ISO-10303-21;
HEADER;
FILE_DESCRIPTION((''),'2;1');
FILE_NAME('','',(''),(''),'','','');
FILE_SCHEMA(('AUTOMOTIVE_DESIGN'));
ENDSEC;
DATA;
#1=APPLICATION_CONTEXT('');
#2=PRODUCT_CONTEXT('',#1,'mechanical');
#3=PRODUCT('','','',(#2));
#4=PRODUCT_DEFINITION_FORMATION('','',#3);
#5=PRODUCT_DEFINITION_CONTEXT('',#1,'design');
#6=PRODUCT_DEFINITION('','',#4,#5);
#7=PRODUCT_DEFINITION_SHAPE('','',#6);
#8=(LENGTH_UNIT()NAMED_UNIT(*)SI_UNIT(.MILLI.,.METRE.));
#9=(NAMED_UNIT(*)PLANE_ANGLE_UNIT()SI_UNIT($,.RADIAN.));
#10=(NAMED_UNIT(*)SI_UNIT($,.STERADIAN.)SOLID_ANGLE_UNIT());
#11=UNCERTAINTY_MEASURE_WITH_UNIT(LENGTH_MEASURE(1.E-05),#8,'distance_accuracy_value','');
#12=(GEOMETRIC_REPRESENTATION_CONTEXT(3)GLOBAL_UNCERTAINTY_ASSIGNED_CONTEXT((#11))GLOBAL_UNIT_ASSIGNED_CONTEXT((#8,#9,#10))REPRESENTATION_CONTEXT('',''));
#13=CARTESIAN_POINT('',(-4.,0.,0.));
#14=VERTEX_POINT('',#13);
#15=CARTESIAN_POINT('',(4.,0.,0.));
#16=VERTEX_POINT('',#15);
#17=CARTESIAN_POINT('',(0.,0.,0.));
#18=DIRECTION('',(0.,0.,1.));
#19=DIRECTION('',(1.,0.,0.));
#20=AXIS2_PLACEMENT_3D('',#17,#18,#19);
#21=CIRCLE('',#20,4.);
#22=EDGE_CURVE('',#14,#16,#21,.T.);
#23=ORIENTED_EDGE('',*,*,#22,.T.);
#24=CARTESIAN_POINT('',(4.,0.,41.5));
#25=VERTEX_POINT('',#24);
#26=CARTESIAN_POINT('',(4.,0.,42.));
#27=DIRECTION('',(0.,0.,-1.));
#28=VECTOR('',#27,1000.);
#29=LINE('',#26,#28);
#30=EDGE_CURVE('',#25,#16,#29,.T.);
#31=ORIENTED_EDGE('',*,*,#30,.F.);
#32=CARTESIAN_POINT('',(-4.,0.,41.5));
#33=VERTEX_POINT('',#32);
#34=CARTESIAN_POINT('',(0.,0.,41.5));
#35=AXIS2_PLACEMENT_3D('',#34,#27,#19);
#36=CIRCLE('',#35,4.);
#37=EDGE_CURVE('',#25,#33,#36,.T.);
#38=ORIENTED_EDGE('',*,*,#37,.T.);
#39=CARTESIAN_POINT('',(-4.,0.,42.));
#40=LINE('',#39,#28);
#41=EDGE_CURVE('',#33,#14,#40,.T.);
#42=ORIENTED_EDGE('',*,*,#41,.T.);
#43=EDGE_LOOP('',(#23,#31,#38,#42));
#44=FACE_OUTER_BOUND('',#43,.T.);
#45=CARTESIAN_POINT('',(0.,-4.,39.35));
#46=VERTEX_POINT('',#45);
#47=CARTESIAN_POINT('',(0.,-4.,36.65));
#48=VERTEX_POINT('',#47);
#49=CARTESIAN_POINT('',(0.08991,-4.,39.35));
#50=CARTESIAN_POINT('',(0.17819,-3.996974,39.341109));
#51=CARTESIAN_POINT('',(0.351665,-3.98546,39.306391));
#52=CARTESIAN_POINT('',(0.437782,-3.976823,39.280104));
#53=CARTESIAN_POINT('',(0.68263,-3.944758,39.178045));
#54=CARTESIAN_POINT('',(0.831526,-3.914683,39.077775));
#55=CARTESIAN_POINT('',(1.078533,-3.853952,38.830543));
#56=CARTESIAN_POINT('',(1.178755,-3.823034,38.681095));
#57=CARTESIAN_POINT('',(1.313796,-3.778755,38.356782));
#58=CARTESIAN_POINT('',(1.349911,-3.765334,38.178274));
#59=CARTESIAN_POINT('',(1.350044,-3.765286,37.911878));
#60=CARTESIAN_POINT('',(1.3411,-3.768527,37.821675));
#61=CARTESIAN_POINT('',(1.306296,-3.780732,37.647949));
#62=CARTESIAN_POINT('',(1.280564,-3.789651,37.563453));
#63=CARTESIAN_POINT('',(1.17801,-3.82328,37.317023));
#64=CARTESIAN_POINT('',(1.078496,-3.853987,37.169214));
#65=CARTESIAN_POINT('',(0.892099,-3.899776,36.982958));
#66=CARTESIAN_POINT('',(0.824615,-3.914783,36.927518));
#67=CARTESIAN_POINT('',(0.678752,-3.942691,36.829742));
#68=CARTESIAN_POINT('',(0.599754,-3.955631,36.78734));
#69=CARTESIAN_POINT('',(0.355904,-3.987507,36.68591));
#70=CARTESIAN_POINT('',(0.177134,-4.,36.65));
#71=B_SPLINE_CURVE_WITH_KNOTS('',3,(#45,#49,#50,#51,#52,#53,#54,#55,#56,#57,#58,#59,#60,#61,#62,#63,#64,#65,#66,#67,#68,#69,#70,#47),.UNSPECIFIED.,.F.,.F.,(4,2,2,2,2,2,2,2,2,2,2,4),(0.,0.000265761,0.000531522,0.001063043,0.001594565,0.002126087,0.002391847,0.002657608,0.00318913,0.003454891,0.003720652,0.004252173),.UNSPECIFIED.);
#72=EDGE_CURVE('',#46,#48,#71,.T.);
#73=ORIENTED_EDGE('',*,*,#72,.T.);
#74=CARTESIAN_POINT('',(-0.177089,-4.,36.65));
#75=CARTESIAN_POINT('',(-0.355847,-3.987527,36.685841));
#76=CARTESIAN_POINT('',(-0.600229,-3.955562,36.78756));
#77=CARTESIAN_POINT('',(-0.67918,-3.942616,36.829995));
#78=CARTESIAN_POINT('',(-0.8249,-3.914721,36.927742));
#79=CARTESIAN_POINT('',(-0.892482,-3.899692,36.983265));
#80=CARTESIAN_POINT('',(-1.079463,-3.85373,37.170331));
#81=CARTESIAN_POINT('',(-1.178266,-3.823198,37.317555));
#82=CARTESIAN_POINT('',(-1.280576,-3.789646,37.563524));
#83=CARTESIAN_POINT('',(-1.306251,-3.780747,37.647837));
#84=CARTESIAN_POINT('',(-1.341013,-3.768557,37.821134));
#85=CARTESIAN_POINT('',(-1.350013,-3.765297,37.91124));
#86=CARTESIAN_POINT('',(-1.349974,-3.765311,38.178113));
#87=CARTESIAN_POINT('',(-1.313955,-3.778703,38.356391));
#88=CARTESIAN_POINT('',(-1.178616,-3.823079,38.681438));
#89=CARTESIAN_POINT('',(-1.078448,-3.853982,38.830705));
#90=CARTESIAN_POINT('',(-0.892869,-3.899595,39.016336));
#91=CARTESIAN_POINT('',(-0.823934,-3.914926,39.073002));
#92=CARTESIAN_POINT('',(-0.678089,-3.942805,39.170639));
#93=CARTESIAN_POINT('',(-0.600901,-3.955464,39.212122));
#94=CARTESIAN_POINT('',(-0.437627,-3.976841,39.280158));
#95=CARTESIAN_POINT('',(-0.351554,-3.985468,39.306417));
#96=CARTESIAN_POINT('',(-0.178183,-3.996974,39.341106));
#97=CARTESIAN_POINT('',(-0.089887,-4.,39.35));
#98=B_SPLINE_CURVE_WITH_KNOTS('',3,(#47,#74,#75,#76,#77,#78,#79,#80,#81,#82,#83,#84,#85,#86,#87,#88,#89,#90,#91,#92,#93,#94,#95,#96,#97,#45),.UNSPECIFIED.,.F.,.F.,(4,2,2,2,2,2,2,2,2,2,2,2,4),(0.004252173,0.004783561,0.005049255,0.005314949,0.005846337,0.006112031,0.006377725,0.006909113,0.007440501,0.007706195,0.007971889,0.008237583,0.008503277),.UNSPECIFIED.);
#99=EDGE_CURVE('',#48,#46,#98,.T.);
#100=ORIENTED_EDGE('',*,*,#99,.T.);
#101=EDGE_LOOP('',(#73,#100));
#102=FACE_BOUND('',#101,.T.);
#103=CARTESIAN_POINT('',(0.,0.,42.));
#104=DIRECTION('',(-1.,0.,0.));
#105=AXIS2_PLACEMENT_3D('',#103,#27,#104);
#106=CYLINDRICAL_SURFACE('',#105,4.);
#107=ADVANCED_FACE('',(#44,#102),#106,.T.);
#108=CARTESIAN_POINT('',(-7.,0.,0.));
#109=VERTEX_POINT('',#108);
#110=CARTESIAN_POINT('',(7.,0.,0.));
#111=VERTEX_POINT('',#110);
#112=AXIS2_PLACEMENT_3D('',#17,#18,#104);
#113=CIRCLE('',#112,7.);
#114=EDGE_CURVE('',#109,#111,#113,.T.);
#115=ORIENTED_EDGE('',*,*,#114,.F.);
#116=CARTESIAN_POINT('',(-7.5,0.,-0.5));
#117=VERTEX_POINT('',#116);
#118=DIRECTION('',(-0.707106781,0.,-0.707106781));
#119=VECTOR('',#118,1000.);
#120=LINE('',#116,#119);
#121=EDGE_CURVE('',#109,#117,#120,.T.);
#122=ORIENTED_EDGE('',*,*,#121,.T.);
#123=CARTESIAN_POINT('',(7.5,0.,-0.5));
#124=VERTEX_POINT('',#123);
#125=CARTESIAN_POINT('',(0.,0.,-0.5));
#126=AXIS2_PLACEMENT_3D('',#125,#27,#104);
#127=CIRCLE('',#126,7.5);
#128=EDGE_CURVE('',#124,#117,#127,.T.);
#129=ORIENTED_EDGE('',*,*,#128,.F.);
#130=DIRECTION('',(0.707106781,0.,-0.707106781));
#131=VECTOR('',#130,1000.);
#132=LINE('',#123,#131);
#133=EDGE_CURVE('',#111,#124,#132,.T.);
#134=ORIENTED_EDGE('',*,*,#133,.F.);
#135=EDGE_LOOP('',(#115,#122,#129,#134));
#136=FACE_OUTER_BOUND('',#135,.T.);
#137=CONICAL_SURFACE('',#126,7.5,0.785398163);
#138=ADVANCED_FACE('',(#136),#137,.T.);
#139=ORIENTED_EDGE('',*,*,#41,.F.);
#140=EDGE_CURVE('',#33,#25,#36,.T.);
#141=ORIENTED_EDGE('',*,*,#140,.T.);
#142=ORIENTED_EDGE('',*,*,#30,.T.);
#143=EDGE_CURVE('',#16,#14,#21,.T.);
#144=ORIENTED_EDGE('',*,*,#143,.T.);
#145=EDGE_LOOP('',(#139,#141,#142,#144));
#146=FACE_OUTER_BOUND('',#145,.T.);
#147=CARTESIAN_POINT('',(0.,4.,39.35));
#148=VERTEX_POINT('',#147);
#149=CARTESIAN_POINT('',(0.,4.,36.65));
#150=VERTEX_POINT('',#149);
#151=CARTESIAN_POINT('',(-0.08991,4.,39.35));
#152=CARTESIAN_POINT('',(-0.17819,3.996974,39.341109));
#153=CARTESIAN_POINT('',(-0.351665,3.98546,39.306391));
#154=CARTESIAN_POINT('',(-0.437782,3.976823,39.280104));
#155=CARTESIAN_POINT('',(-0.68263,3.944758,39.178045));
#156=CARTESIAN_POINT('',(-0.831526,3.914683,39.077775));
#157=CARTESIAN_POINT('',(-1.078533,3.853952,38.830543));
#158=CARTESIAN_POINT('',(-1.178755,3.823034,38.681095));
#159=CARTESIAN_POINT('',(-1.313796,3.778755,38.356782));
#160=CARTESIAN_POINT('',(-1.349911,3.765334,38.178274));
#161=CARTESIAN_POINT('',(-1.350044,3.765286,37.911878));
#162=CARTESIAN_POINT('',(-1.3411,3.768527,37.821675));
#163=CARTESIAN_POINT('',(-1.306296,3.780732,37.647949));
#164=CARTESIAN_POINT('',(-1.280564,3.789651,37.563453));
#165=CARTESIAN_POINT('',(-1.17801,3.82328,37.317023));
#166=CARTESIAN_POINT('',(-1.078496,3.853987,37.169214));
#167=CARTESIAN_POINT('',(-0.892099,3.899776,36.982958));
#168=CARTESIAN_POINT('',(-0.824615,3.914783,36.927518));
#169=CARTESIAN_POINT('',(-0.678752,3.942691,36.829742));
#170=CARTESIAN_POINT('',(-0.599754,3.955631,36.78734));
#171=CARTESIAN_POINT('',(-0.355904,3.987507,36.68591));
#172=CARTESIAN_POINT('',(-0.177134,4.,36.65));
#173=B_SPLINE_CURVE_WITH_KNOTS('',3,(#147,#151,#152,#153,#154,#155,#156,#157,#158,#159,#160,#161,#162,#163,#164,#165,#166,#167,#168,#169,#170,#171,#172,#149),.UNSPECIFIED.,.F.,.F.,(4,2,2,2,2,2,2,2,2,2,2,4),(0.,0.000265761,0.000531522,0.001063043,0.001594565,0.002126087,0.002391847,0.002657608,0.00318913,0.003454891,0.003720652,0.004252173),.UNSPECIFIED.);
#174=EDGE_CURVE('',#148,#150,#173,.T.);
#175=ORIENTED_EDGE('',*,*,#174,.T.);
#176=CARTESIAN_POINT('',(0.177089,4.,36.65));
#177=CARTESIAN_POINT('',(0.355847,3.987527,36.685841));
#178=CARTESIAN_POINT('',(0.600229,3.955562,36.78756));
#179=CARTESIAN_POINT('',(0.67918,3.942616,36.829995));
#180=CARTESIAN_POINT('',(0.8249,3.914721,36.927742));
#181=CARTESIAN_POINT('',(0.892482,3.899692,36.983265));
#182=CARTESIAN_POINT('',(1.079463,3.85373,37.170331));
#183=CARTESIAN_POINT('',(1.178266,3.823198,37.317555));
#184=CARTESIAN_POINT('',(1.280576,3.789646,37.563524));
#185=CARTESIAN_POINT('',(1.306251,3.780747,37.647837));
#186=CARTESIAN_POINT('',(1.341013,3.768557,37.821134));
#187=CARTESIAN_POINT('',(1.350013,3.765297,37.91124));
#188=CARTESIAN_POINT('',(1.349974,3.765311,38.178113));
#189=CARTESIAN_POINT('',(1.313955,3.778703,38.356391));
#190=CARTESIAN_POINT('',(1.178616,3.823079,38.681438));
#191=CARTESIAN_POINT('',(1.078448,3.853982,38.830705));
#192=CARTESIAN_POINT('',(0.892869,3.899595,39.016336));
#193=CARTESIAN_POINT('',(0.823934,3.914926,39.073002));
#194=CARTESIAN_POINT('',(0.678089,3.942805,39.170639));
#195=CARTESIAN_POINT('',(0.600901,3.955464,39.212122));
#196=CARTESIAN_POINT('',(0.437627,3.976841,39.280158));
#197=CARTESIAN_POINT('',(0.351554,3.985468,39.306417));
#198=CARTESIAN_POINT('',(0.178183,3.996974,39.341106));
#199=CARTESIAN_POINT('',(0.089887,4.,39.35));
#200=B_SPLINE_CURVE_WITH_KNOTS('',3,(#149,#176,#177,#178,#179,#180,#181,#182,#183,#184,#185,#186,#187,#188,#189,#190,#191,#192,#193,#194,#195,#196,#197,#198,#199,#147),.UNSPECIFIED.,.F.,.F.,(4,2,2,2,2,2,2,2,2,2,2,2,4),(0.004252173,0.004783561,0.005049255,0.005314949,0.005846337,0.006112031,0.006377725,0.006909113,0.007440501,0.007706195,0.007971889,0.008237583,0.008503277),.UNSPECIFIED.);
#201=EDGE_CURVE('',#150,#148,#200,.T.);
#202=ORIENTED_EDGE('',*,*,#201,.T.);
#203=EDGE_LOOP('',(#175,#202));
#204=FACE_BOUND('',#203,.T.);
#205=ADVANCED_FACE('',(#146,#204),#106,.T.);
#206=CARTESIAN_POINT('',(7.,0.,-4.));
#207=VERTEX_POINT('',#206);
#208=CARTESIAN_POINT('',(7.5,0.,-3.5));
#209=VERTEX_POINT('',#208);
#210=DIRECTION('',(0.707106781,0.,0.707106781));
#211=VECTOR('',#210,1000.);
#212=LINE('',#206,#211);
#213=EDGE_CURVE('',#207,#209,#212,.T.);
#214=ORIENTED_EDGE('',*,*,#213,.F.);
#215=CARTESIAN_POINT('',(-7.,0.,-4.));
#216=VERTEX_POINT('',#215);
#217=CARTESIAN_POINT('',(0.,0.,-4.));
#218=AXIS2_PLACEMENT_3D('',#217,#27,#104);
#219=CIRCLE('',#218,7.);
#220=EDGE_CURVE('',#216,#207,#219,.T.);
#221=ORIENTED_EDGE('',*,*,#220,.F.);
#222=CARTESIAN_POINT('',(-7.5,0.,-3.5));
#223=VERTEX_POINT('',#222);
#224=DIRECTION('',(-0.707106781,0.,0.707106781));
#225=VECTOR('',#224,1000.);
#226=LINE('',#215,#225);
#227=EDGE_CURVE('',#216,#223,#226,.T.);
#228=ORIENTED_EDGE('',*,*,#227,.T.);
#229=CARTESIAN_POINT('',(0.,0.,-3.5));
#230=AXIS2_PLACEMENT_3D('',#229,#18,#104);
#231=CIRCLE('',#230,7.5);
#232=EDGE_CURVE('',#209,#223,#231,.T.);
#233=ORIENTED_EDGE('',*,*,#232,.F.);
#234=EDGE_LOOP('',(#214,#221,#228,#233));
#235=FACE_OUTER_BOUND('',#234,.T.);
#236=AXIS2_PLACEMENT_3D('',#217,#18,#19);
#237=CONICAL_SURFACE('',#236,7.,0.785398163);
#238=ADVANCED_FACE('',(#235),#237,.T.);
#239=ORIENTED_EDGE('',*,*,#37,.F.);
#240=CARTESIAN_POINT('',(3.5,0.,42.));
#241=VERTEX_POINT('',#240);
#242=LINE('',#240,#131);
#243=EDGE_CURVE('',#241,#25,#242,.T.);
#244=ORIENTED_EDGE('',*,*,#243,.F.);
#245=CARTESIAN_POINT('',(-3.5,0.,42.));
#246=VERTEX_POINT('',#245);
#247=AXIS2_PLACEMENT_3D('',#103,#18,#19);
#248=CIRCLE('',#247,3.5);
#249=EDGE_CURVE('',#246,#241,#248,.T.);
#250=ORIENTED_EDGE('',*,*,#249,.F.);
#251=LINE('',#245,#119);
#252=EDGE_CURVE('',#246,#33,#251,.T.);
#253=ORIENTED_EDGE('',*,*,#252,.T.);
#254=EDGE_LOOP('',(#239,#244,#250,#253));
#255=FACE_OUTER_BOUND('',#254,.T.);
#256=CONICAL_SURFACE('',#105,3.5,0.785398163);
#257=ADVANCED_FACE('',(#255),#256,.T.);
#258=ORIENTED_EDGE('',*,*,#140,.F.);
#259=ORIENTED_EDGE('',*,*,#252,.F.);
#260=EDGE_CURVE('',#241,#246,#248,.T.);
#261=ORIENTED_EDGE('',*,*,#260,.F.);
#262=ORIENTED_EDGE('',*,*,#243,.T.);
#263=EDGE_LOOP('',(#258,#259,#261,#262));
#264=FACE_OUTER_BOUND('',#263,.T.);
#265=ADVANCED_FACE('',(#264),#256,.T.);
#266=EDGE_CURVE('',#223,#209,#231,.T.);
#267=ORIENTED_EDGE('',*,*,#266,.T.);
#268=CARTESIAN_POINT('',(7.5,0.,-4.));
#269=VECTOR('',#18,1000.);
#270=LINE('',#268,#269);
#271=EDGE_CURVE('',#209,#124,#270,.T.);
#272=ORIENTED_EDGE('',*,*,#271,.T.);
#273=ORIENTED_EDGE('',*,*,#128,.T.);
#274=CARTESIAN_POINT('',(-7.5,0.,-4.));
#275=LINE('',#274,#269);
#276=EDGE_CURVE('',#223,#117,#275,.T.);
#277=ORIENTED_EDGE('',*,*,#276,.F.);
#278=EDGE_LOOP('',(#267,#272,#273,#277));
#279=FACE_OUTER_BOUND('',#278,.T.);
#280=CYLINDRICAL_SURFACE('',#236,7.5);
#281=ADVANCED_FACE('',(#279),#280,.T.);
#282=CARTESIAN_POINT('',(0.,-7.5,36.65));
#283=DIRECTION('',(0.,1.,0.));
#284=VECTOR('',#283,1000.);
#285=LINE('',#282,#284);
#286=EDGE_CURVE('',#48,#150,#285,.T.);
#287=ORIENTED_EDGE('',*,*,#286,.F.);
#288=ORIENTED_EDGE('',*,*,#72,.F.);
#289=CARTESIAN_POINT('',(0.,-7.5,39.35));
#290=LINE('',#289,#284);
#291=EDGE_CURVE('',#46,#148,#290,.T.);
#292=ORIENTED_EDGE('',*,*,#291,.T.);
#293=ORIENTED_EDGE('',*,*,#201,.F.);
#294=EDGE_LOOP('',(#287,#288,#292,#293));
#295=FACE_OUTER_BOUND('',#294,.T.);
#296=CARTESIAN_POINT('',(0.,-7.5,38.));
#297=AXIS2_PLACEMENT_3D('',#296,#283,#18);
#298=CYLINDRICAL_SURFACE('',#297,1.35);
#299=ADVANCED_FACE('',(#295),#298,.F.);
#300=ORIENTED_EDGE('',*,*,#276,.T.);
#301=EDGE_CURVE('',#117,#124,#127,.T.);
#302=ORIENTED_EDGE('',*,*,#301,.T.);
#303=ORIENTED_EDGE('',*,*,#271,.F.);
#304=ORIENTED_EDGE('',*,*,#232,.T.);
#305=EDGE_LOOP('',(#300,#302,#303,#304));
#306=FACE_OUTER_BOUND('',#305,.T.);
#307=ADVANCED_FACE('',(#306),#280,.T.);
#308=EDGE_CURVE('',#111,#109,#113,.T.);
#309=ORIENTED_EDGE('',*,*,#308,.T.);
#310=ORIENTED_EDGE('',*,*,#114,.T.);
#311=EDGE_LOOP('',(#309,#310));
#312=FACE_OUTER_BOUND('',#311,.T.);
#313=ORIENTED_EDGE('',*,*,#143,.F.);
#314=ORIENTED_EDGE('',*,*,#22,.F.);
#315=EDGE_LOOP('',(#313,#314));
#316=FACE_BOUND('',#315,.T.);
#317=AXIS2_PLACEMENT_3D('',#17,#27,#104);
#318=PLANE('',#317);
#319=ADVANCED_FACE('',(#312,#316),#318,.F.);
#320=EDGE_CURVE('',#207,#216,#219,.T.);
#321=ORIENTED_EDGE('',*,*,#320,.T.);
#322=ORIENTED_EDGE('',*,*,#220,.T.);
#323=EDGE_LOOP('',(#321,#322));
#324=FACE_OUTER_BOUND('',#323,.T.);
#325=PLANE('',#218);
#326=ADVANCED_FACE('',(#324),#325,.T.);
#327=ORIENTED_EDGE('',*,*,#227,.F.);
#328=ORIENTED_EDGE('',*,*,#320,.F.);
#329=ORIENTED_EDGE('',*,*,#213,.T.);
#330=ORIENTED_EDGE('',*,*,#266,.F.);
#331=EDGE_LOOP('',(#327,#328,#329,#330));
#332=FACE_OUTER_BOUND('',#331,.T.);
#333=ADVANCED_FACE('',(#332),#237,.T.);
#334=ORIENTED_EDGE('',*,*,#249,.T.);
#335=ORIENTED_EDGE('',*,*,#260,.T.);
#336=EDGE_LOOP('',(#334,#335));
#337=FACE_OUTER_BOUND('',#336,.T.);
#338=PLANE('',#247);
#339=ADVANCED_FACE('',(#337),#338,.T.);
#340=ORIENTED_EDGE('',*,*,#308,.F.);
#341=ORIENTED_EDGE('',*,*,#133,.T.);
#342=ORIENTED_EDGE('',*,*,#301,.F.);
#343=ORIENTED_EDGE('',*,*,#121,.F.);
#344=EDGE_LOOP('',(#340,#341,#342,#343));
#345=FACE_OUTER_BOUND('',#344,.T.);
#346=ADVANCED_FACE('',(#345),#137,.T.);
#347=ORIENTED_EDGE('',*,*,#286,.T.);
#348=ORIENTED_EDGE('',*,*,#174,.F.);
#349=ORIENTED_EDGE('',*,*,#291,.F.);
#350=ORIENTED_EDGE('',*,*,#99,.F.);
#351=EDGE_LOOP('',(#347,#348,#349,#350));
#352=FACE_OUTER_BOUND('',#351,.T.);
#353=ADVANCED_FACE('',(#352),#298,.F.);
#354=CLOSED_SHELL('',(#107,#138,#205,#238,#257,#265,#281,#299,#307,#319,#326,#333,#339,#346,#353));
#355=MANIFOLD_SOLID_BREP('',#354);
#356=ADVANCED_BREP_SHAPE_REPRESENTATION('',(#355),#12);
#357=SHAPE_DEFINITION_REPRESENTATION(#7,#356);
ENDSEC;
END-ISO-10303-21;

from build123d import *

# Parameters (mm, degrees)
SKETCH1_R               = 4
BOSS_EXTRUDE1_DEPTH     = 42
SKETCH2_R               = 7.5
BOSS_EXTRUDE2_DEPTH     = 4
CUT_EXTRUDE1_DEPTH      = 44.318587235
CUT_EXTRUDE1_DEPTH_BACK = 44.318587235
SKETCH3_R               = 1.35
CHAMFER1_SIZE           = 0.5


with BuildPart() as part:
    # Sketch1 → Boss-Extrude1 (new body)
    with BuildSketch(Plane.XY):
        with Locations(Location((0, 0, 0), (0, 0, 180))):
            Circle(SKETCH1_R)
    extrude(amount=BOSS_EXTRUDE1_DEPTH)

    # Sketch2 → Boss-Extrude2 (add)
    with BuildSketch(Plane(origin=(0, 0, 0), x_dir=(-1, 0, 0), z_dir=(0, 0, -1))):
        Circle(SKETCH2_R)
    extrude(amount=BOSS_EXTRUDE2_DEPTH)

    # Sketch3 → Cut-Extrude1 (cut, two sides: drawn at the far end of the back side and taken through both)
    with BuildSketch(Plane(origin=(0, 0, 0), x_dir=(1, 0, 0), z_dir=(0, 1, 0)).offset(-CUT_EXTRUDE1_DEPTH_BACK)):
        with Locations(Location((0, -38, 0), (0, 0, 270))):
            Circle(SKETCH3_R)
    extrude(amount=CUT_EXTRUDE1_DEPTH + CUT_EXTRUDE1_DEPTH_BACK, mode=Mode.SUBTRACT)

    # Chamfer1
    chamfer1_edges = [part.edges().sort_by_distance(p)[0] for p in [
        (4, 0, 42),
        (7.5, 0, 0),
        (7.5, 0, -4),
    ]]
    chamfer(chamfer1_edges, length=CHAMFER1_SIZE)


solid = part.part
